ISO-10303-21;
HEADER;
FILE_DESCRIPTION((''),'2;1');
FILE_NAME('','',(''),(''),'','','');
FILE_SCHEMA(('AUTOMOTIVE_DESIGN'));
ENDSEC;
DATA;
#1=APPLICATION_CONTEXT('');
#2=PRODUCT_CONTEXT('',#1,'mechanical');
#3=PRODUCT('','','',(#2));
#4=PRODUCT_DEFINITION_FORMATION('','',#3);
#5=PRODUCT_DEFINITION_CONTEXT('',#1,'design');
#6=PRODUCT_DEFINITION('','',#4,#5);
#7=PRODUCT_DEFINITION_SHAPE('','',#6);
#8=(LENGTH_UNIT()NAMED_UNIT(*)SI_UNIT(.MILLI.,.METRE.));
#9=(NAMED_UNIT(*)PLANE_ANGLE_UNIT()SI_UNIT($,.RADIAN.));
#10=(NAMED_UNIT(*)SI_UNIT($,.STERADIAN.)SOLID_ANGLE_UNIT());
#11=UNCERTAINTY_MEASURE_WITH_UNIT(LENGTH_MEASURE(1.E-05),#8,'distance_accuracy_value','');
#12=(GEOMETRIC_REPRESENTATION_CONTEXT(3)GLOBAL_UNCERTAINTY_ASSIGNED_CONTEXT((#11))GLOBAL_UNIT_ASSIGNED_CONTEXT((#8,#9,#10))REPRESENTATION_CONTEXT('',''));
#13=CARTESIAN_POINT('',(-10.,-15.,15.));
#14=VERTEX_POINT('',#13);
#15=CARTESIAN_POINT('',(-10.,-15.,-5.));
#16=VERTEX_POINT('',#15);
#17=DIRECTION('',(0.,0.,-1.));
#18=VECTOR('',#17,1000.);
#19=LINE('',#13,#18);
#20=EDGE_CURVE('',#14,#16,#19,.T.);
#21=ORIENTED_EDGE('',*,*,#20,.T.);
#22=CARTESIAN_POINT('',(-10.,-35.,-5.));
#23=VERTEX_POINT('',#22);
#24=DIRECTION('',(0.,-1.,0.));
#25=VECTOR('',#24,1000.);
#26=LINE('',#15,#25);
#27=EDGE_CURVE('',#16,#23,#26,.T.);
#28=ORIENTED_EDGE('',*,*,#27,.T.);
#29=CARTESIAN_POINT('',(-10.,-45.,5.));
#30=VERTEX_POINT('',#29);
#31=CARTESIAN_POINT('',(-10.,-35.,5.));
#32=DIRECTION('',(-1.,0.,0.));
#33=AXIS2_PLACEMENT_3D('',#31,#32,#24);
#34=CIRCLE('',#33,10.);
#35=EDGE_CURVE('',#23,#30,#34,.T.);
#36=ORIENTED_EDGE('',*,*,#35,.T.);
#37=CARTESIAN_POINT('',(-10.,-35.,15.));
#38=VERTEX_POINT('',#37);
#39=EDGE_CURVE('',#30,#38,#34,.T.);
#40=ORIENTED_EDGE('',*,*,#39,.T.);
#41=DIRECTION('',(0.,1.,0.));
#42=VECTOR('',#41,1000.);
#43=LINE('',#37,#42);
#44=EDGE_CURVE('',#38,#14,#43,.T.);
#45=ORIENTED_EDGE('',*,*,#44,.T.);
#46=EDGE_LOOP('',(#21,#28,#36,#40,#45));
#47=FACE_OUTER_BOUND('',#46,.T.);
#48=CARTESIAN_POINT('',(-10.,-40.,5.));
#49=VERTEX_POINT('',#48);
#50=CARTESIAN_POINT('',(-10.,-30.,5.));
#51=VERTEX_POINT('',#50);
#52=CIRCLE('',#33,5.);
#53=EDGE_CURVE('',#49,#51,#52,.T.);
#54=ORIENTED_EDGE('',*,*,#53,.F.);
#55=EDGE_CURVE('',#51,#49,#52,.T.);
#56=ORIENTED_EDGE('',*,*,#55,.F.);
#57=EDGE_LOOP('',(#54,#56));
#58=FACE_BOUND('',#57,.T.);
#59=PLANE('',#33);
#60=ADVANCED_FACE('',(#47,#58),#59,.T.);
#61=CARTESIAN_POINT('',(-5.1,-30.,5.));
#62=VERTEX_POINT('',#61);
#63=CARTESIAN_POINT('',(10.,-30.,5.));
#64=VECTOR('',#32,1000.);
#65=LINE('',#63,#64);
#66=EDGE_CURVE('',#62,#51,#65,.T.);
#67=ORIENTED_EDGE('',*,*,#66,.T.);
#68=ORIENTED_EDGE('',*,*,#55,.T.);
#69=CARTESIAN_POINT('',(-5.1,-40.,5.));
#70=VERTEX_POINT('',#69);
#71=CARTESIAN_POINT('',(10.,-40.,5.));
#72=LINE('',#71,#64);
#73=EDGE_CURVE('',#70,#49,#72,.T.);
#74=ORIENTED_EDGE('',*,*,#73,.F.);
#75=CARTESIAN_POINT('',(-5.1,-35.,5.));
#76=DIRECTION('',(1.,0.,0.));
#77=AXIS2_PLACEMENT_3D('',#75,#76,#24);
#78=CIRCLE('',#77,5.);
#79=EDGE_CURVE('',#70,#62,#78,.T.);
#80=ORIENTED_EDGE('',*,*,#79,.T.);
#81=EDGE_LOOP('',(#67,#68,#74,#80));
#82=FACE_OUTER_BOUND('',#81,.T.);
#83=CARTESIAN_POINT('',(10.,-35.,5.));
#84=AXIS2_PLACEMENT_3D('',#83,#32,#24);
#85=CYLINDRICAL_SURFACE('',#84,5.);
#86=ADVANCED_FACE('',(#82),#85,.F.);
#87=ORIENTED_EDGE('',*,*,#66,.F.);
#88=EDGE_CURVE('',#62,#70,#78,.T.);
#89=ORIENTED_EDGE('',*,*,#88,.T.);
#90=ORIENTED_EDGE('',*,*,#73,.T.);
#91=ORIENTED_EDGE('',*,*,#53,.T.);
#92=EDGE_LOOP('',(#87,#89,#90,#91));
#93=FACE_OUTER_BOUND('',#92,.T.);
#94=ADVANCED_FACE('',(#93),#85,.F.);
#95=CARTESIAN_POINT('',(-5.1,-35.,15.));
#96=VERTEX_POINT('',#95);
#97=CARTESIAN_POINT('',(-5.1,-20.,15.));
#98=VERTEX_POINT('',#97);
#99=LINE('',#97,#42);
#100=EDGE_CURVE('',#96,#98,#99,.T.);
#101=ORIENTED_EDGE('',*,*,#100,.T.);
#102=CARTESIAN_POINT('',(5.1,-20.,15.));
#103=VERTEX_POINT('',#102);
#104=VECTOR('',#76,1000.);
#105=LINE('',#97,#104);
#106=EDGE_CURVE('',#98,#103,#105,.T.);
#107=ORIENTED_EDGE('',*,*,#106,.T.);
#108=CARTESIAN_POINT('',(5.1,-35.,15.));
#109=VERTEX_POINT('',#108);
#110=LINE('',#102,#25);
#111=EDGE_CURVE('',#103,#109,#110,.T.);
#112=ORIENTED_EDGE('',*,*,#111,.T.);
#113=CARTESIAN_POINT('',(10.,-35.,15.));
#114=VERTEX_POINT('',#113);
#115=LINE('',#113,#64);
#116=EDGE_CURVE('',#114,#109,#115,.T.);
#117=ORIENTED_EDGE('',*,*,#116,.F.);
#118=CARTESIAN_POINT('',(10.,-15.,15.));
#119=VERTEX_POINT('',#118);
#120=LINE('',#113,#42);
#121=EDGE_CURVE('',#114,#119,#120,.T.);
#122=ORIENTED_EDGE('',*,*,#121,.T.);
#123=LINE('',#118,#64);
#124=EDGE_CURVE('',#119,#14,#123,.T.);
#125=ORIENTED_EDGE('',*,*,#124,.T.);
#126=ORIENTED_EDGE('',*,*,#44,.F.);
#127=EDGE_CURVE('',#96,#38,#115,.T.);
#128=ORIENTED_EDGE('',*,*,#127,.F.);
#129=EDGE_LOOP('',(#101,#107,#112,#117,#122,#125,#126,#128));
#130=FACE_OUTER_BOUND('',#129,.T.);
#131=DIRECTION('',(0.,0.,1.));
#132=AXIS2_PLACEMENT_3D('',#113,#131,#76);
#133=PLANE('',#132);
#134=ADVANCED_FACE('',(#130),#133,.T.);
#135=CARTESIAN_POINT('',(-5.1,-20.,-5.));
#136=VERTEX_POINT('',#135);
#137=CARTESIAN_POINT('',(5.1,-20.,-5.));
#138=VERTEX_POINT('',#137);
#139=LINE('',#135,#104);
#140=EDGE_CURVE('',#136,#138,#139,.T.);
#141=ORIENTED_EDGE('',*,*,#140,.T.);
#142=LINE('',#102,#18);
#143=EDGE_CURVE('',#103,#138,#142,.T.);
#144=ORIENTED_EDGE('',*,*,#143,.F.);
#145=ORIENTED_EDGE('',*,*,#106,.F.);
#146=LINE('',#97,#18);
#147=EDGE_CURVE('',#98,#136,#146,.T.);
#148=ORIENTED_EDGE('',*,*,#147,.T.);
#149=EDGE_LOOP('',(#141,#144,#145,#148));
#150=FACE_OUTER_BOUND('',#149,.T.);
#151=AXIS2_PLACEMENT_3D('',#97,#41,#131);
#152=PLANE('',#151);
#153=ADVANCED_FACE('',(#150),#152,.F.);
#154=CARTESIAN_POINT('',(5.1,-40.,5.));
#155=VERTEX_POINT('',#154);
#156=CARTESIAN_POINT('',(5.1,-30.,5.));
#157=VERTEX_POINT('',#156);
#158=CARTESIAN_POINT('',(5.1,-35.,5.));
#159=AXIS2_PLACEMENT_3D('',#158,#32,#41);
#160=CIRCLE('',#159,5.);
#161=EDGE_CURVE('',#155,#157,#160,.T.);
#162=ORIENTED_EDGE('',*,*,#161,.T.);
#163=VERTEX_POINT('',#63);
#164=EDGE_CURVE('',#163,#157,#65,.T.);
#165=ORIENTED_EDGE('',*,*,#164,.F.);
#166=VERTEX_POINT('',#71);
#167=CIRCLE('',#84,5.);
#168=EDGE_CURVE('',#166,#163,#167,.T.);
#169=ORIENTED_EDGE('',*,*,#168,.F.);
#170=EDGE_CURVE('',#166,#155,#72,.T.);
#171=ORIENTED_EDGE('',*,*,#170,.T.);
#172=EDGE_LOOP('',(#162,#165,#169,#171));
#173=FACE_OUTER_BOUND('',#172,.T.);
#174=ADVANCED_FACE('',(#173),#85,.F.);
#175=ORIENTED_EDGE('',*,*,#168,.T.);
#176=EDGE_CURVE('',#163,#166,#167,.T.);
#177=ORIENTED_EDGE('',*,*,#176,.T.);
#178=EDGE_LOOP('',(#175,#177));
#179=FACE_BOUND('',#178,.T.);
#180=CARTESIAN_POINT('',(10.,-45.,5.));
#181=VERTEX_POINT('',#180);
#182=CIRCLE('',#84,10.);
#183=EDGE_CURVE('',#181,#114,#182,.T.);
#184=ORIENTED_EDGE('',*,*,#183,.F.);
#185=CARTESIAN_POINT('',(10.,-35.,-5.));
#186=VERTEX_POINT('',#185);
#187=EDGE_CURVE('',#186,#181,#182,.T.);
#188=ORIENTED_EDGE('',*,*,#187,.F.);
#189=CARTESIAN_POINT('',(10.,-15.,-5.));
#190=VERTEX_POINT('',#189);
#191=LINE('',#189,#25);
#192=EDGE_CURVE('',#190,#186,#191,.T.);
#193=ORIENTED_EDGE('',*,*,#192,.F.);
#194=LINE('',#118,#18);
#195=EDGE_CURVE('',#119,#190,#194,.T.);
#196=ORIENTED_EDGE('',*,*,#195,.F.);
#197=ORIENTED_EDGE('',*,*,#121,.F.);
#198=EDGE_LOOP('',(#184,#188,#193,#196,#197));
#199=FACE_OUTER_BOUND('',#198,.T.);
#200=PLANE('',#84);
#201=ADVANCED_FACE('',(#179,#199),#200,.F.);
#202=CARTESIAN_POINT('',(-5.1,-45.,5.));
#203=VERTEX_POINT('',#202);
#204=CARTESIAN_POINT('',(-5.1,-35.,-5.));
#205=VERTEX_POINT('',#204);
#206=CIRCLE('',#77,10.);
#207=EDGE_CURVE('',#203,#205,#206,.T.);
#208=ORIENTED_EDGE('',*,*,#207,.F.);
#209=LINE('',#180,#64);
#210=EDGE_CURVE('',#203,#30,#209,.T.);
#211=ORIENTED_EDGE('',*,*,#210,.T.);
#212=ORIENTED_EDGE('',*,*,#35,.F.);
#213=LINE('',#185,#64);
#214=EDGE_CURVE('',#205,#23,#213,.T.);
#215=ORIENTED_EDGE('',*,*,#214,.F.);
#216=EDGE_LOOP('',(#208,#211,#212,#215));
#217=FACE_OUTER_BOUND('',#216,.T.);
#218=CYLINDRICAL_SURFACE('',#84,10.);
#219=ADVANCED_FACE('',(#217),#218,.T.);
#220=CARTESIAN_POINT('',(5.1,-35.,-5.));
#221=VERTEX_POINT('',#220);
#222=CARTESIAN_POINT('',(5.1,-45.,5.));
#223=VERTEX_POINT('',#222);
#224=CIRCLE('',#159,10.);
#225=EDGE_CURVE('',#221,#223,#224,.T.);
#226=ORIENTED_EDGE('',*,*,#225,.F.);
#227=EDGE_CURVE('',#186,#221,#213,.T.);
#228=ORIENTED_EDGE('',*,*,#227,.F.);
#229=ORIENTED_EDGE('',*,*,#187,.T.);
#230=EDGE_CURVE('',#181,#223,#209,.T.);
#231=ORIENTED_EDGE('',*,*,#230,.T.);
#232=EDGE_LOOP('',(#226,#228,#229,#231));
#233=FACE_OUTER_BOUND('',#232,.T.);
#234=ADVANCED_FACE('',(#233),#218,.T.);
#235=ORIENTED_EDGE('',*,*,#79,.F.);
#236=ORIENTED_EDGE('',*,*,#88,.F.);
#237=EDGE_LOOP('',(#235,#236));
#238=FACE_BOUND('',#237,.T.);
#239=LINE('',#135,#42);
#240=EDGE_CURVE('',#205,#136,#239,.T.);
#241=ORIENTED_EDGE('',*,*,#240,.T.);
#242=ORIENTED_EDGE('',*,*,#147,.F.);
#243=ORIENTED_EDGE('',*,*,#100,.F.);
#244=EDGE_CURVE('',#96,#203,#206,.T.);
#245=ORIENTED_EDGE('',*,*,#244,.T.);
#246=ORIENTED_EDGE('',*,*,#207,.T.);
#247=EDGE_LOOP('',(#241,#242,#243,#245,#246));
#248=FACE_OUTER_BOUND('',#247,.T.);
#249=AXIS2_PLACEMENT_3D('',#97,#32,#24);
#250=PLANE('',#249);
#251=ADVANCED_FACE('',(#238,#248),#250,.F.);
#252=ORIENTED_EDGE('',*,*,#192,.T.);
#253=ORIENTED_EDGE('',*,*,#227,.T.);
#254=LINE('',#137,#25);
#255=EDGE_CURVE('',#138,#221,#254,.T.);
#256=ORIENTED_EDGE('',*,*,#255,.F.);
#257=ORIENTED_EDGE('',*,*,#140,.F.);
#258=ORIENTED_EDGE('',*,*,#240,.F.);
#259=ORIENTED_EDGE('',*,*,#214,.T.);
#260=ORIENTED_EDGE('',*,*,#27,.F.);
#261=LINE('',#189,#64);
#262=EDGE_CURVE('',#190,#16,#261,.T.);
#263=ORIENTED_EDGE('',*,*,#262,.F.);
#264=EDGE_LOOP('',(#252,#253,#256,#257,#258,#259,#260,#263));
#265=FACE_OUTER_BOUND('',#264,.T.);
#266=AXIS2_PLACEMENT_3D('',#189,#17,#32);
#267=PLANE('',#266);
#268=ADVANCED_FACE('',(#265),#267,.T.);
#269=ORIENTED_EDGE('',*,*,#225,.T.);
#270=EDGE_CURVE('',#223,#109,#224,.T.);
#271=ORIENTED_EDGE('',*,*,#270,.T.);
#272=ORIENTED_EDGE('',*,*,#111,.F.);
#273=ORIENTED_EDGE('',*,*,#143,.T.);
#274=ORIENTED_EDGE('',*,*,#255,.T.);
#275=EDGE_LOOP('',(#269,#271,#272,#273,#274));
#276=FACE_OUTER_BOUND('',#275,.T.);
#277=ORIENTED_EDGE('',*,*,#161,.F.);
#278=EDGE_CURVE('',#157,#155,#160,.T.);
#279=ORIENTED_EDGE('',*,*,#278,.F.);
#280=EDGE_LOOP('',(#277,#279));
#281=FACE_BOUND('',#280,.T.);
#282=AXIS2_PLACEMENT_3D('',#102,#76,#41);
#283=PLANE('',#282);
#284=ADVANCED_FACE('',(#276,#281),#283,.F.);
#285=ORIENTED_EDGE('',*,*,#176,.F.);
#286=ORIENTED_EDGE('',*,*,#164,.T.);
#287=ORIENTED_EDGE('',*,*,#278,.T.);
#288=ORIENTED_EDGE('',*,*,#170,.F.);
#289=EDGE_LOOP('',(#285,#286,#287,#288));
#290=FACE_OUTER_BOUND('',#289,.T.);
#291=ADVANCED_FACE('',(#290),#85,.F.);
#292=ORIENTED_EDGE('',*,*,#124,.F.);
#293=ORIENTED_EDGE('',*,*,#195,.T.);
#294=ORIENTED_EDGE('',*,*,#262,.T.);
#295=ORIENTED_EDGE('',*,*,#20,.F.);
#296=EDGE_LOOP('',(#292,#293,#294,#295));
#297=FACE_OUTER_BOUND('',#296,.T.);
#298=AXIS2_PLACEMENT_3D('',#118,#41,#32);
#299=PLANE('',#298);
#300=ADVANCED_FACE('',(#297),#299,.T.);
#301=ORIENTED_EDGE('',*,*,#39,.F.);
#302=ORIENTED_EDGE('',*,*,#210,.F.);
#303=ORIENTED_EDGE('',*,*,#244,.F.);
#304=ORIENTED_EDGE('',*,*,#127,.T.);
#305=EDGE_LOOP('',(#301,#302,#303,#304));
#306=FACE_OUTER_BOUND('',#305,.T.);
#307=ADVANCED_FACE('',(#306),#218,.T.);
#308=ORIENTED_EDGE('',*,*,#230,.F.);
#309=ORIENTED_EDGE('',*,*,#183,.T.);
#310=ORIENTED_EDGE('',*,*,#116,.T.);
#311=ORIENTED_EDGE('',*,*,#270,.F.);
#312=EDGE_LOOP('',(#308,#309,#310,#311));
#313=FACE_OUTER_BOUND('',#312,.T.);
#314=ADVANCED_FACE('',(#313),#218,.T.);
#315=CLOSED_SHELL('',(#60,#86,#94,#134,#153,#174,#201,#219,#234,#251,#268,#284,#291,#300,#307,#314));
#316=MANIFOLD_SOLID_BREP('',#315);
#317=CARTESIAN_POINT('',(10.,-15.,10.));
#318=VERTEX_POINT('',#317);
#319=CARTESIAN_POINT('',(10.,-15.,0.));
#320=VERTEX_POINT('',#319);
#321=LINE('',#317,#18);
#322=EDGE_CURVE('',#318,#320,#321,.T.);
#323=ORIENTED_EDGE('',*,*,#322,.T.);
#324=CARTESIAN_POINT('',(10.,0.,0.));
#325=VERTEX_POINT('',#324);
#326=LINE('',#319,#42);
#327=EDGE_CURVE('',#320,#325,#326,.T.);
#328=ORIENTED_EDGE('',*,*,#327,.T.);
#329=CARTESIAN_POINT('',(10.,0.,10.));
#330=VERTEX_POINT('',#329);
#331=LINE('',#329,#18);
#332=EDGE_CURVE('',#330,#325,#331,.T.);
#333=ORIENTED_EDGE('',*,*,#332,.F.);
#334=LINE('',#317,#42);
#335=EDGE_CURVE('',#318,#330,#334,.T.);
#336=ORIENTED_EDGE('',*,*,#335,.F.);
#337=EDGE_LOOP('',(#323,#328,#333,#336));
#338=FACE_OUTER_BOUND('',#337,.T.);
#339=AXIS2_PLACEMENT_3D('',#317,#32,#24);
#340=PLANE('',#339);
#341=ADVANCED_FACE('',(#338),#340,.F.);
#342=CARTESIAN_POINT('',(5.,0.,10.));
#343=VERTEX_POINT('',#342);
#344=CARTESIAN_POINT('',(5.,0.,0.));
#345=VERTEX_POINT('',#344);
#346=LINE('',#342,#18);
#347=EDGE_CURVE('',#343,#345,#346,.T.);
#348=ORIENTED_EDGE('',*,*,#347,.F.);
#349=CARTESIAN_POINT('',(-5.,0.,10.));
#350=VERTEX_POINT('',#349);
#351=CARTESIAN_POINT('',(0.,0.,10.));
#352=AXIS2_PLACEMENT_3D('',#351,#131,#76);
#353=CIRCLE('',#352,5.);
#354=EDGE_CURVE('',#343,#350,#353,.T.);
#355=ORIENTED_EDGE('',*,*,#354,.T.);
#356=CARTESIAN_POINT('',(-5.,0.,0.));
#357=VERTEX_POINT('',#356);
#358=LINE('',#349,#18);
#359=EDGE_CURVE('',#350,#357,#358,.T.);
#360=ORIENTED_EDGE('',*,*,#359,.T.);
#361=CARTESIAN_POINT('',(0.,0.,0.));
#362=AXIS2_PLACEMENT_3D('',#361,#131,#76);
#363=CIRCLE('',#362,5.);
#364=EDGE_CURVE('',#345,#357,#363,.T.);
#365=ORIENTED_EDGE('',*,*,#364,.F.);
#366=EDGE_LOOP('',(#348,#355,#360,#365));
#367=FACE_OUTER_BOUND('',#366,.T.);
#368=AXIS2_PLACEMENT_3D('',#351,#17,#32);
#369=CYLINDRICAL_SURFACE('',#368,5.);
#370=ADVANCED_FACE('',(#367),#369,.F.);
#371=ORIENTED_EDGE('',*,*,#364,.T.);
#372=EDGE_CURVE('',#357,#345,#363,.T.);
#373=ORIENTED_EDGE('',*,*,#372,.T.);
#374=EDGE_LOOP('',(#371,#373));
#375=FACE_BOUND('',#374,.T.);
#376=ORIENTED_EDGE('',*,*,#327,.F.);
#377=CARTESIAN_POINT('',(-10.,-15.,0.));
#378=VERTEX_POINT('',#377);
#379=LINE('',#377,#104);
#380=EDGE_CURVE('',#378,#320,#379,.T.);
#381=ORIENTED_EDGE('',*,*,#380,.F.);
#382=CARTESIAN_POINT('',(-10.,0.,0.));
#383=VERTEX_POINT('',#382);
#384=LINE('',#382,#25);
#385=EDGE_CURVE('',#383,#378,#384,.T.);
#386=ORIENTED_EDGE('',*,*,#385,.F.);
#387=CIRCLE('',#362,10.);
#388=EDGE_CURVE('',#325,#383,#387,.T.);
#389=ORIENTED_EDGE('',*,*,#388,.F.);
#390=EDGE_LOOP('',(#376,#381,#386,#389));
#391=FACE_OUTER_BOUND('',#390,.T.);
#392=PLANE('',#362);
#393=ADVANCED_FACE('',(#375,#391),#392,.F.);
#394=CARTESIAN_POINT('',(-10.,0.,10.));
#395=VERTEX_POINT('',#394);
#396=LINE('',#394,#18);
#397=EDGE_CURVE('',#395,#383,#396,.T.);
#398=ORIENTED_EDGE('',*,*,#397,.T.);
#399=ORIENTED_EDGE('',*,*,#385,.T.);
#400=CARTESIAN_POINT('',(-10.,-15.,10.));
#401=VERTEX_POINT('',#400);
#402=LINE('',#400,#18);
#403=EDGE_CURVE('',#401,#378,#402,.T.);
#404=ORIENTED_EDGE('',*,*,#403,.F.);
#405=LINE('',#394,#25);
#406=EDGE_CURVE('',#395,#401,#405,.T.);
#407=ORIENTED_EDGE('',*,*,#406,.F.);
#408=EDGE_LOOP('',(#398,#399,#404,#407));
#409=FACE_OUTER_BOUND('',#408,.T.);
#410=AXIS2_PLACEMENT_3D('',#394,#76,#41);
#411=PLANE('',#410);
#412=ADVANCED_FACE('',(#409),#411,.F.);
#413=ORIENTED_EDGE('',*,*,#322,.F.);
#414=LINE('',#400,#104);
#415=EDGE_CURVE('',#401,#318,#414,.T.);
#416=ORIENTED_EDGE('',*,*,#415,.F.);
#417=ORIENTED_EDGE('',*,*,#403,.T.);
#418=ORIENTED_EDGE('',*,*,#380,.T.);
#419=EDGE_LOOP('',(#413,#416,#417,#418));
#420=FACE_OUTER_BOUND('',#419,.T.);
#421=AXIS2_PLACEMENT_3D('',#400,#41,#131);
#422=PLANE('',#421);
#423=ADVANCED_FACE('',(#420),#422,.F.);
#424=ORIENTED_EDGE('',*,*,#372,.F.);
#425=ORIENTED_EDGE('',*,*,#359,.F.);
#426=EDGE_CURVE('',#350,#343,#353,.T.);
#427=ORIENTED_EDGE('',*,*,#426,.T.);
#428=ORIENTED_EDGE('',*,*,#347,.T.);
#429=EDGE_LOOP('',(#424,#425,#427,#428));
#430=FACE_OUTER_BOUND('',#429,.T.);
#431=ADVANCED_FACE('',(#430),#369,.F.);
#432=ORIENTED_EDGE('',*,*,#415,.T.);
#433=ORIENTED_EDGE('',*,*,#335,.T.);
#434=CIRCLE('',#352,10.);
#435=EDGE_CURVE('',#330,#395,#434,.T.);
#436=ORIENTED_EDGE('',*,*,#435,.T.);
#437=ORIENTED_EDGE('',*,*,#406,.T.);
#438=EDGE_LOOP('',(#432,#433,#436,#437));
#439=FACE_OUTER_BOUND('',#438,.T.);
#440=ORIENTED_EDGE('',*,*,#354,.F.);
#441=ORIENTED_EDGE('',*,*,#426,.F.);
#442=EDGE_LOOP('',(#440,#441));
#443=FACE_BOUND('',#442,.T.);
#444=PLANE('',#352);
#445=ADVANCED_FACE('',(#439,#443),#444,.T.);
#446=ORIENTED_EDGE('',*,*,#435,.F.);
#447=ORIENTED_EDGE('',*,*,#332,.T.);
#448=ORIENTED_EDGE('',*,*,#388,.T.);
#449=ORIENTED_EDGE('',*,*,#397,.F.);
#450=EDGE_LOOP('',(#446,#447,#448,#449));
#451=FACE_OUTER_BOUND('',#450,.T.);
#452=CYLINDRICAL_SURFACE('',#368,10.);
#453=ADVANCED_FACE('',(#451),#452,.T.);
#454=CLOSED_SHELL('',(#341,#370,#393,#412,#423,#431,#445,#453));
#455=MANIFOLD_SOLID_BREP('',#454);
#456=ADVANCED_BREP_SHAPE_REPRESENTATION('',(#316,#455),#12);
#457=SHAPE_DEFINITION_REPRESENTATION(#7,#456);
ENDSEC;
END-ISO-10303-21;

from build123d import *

# Parameters (mm, degrees)
SKETCH1_R           = 5
BOSS_EXTRUDE1_DEPTH = 10
SKETCH2_R           = 5
BOSS_EXTRUDE2_DEPTH = 20
SKETCH3_W           = 10.2
SKETCH3_H           = 29.458031572
CUT_EXTRUDE1_DEPTH  = 51.249378106


with BuildPart() as part:
    # Sketch1 → Boss-Extrude1 (new body)
    with BuildSketch(Plane.XY):
        with BuildLine():
            Line((-10, 0), (-10, -15))
            Line((-10, -15), (10, -15))
            Line((10, -15), (10, 0))
            ThreePointArc((10, 0), (0, 10), (-10, 0))
        make_face()
        Circle(SKETCH1_R, mode=Mode.SUBTRACT)
    extrude(amount=BOSS_EXTRUDE1_DEPTH)


with BuildPart() as body_2:
    # Sketch2 → Boss-Extrude2 (new body)
    with BuildSketch(Plane.ZY.offset(10)):
        with BuildLine():
            Line((15, -35), (15, -15))
            Line((15, -15), (-5, -15))
            Line((-5, -15), (-5, -35))
            ThreePointArc((-5, -35), (5, -45), (15, -35))
        make_face()
        with Locations(Location((5, -35, 0), (0, 0, 270))):
            Circle(SKETCH2_R, mode=Mode.SUBTRACT)
    extrude(amount=-BOSS_EXTRUDE2_DEPTH)

    # Sketch3 → Cut-Extrude1 (cut, through all)
    with BuildSketch(Plane(origin=(0, 0, -5), x_dir=(-1, 0, 0), z_dir=(0, 0, -1))):
        with Locations((0, -34.729015786)):
            Rectangle(SKETCH3_W, SKETCH3_H)
    extrude(amount=-CUT_EXTRUDE1_DEPTH, mode=Mode.SUBTRACT)


solid = Compound([part.part, body_2.part])
